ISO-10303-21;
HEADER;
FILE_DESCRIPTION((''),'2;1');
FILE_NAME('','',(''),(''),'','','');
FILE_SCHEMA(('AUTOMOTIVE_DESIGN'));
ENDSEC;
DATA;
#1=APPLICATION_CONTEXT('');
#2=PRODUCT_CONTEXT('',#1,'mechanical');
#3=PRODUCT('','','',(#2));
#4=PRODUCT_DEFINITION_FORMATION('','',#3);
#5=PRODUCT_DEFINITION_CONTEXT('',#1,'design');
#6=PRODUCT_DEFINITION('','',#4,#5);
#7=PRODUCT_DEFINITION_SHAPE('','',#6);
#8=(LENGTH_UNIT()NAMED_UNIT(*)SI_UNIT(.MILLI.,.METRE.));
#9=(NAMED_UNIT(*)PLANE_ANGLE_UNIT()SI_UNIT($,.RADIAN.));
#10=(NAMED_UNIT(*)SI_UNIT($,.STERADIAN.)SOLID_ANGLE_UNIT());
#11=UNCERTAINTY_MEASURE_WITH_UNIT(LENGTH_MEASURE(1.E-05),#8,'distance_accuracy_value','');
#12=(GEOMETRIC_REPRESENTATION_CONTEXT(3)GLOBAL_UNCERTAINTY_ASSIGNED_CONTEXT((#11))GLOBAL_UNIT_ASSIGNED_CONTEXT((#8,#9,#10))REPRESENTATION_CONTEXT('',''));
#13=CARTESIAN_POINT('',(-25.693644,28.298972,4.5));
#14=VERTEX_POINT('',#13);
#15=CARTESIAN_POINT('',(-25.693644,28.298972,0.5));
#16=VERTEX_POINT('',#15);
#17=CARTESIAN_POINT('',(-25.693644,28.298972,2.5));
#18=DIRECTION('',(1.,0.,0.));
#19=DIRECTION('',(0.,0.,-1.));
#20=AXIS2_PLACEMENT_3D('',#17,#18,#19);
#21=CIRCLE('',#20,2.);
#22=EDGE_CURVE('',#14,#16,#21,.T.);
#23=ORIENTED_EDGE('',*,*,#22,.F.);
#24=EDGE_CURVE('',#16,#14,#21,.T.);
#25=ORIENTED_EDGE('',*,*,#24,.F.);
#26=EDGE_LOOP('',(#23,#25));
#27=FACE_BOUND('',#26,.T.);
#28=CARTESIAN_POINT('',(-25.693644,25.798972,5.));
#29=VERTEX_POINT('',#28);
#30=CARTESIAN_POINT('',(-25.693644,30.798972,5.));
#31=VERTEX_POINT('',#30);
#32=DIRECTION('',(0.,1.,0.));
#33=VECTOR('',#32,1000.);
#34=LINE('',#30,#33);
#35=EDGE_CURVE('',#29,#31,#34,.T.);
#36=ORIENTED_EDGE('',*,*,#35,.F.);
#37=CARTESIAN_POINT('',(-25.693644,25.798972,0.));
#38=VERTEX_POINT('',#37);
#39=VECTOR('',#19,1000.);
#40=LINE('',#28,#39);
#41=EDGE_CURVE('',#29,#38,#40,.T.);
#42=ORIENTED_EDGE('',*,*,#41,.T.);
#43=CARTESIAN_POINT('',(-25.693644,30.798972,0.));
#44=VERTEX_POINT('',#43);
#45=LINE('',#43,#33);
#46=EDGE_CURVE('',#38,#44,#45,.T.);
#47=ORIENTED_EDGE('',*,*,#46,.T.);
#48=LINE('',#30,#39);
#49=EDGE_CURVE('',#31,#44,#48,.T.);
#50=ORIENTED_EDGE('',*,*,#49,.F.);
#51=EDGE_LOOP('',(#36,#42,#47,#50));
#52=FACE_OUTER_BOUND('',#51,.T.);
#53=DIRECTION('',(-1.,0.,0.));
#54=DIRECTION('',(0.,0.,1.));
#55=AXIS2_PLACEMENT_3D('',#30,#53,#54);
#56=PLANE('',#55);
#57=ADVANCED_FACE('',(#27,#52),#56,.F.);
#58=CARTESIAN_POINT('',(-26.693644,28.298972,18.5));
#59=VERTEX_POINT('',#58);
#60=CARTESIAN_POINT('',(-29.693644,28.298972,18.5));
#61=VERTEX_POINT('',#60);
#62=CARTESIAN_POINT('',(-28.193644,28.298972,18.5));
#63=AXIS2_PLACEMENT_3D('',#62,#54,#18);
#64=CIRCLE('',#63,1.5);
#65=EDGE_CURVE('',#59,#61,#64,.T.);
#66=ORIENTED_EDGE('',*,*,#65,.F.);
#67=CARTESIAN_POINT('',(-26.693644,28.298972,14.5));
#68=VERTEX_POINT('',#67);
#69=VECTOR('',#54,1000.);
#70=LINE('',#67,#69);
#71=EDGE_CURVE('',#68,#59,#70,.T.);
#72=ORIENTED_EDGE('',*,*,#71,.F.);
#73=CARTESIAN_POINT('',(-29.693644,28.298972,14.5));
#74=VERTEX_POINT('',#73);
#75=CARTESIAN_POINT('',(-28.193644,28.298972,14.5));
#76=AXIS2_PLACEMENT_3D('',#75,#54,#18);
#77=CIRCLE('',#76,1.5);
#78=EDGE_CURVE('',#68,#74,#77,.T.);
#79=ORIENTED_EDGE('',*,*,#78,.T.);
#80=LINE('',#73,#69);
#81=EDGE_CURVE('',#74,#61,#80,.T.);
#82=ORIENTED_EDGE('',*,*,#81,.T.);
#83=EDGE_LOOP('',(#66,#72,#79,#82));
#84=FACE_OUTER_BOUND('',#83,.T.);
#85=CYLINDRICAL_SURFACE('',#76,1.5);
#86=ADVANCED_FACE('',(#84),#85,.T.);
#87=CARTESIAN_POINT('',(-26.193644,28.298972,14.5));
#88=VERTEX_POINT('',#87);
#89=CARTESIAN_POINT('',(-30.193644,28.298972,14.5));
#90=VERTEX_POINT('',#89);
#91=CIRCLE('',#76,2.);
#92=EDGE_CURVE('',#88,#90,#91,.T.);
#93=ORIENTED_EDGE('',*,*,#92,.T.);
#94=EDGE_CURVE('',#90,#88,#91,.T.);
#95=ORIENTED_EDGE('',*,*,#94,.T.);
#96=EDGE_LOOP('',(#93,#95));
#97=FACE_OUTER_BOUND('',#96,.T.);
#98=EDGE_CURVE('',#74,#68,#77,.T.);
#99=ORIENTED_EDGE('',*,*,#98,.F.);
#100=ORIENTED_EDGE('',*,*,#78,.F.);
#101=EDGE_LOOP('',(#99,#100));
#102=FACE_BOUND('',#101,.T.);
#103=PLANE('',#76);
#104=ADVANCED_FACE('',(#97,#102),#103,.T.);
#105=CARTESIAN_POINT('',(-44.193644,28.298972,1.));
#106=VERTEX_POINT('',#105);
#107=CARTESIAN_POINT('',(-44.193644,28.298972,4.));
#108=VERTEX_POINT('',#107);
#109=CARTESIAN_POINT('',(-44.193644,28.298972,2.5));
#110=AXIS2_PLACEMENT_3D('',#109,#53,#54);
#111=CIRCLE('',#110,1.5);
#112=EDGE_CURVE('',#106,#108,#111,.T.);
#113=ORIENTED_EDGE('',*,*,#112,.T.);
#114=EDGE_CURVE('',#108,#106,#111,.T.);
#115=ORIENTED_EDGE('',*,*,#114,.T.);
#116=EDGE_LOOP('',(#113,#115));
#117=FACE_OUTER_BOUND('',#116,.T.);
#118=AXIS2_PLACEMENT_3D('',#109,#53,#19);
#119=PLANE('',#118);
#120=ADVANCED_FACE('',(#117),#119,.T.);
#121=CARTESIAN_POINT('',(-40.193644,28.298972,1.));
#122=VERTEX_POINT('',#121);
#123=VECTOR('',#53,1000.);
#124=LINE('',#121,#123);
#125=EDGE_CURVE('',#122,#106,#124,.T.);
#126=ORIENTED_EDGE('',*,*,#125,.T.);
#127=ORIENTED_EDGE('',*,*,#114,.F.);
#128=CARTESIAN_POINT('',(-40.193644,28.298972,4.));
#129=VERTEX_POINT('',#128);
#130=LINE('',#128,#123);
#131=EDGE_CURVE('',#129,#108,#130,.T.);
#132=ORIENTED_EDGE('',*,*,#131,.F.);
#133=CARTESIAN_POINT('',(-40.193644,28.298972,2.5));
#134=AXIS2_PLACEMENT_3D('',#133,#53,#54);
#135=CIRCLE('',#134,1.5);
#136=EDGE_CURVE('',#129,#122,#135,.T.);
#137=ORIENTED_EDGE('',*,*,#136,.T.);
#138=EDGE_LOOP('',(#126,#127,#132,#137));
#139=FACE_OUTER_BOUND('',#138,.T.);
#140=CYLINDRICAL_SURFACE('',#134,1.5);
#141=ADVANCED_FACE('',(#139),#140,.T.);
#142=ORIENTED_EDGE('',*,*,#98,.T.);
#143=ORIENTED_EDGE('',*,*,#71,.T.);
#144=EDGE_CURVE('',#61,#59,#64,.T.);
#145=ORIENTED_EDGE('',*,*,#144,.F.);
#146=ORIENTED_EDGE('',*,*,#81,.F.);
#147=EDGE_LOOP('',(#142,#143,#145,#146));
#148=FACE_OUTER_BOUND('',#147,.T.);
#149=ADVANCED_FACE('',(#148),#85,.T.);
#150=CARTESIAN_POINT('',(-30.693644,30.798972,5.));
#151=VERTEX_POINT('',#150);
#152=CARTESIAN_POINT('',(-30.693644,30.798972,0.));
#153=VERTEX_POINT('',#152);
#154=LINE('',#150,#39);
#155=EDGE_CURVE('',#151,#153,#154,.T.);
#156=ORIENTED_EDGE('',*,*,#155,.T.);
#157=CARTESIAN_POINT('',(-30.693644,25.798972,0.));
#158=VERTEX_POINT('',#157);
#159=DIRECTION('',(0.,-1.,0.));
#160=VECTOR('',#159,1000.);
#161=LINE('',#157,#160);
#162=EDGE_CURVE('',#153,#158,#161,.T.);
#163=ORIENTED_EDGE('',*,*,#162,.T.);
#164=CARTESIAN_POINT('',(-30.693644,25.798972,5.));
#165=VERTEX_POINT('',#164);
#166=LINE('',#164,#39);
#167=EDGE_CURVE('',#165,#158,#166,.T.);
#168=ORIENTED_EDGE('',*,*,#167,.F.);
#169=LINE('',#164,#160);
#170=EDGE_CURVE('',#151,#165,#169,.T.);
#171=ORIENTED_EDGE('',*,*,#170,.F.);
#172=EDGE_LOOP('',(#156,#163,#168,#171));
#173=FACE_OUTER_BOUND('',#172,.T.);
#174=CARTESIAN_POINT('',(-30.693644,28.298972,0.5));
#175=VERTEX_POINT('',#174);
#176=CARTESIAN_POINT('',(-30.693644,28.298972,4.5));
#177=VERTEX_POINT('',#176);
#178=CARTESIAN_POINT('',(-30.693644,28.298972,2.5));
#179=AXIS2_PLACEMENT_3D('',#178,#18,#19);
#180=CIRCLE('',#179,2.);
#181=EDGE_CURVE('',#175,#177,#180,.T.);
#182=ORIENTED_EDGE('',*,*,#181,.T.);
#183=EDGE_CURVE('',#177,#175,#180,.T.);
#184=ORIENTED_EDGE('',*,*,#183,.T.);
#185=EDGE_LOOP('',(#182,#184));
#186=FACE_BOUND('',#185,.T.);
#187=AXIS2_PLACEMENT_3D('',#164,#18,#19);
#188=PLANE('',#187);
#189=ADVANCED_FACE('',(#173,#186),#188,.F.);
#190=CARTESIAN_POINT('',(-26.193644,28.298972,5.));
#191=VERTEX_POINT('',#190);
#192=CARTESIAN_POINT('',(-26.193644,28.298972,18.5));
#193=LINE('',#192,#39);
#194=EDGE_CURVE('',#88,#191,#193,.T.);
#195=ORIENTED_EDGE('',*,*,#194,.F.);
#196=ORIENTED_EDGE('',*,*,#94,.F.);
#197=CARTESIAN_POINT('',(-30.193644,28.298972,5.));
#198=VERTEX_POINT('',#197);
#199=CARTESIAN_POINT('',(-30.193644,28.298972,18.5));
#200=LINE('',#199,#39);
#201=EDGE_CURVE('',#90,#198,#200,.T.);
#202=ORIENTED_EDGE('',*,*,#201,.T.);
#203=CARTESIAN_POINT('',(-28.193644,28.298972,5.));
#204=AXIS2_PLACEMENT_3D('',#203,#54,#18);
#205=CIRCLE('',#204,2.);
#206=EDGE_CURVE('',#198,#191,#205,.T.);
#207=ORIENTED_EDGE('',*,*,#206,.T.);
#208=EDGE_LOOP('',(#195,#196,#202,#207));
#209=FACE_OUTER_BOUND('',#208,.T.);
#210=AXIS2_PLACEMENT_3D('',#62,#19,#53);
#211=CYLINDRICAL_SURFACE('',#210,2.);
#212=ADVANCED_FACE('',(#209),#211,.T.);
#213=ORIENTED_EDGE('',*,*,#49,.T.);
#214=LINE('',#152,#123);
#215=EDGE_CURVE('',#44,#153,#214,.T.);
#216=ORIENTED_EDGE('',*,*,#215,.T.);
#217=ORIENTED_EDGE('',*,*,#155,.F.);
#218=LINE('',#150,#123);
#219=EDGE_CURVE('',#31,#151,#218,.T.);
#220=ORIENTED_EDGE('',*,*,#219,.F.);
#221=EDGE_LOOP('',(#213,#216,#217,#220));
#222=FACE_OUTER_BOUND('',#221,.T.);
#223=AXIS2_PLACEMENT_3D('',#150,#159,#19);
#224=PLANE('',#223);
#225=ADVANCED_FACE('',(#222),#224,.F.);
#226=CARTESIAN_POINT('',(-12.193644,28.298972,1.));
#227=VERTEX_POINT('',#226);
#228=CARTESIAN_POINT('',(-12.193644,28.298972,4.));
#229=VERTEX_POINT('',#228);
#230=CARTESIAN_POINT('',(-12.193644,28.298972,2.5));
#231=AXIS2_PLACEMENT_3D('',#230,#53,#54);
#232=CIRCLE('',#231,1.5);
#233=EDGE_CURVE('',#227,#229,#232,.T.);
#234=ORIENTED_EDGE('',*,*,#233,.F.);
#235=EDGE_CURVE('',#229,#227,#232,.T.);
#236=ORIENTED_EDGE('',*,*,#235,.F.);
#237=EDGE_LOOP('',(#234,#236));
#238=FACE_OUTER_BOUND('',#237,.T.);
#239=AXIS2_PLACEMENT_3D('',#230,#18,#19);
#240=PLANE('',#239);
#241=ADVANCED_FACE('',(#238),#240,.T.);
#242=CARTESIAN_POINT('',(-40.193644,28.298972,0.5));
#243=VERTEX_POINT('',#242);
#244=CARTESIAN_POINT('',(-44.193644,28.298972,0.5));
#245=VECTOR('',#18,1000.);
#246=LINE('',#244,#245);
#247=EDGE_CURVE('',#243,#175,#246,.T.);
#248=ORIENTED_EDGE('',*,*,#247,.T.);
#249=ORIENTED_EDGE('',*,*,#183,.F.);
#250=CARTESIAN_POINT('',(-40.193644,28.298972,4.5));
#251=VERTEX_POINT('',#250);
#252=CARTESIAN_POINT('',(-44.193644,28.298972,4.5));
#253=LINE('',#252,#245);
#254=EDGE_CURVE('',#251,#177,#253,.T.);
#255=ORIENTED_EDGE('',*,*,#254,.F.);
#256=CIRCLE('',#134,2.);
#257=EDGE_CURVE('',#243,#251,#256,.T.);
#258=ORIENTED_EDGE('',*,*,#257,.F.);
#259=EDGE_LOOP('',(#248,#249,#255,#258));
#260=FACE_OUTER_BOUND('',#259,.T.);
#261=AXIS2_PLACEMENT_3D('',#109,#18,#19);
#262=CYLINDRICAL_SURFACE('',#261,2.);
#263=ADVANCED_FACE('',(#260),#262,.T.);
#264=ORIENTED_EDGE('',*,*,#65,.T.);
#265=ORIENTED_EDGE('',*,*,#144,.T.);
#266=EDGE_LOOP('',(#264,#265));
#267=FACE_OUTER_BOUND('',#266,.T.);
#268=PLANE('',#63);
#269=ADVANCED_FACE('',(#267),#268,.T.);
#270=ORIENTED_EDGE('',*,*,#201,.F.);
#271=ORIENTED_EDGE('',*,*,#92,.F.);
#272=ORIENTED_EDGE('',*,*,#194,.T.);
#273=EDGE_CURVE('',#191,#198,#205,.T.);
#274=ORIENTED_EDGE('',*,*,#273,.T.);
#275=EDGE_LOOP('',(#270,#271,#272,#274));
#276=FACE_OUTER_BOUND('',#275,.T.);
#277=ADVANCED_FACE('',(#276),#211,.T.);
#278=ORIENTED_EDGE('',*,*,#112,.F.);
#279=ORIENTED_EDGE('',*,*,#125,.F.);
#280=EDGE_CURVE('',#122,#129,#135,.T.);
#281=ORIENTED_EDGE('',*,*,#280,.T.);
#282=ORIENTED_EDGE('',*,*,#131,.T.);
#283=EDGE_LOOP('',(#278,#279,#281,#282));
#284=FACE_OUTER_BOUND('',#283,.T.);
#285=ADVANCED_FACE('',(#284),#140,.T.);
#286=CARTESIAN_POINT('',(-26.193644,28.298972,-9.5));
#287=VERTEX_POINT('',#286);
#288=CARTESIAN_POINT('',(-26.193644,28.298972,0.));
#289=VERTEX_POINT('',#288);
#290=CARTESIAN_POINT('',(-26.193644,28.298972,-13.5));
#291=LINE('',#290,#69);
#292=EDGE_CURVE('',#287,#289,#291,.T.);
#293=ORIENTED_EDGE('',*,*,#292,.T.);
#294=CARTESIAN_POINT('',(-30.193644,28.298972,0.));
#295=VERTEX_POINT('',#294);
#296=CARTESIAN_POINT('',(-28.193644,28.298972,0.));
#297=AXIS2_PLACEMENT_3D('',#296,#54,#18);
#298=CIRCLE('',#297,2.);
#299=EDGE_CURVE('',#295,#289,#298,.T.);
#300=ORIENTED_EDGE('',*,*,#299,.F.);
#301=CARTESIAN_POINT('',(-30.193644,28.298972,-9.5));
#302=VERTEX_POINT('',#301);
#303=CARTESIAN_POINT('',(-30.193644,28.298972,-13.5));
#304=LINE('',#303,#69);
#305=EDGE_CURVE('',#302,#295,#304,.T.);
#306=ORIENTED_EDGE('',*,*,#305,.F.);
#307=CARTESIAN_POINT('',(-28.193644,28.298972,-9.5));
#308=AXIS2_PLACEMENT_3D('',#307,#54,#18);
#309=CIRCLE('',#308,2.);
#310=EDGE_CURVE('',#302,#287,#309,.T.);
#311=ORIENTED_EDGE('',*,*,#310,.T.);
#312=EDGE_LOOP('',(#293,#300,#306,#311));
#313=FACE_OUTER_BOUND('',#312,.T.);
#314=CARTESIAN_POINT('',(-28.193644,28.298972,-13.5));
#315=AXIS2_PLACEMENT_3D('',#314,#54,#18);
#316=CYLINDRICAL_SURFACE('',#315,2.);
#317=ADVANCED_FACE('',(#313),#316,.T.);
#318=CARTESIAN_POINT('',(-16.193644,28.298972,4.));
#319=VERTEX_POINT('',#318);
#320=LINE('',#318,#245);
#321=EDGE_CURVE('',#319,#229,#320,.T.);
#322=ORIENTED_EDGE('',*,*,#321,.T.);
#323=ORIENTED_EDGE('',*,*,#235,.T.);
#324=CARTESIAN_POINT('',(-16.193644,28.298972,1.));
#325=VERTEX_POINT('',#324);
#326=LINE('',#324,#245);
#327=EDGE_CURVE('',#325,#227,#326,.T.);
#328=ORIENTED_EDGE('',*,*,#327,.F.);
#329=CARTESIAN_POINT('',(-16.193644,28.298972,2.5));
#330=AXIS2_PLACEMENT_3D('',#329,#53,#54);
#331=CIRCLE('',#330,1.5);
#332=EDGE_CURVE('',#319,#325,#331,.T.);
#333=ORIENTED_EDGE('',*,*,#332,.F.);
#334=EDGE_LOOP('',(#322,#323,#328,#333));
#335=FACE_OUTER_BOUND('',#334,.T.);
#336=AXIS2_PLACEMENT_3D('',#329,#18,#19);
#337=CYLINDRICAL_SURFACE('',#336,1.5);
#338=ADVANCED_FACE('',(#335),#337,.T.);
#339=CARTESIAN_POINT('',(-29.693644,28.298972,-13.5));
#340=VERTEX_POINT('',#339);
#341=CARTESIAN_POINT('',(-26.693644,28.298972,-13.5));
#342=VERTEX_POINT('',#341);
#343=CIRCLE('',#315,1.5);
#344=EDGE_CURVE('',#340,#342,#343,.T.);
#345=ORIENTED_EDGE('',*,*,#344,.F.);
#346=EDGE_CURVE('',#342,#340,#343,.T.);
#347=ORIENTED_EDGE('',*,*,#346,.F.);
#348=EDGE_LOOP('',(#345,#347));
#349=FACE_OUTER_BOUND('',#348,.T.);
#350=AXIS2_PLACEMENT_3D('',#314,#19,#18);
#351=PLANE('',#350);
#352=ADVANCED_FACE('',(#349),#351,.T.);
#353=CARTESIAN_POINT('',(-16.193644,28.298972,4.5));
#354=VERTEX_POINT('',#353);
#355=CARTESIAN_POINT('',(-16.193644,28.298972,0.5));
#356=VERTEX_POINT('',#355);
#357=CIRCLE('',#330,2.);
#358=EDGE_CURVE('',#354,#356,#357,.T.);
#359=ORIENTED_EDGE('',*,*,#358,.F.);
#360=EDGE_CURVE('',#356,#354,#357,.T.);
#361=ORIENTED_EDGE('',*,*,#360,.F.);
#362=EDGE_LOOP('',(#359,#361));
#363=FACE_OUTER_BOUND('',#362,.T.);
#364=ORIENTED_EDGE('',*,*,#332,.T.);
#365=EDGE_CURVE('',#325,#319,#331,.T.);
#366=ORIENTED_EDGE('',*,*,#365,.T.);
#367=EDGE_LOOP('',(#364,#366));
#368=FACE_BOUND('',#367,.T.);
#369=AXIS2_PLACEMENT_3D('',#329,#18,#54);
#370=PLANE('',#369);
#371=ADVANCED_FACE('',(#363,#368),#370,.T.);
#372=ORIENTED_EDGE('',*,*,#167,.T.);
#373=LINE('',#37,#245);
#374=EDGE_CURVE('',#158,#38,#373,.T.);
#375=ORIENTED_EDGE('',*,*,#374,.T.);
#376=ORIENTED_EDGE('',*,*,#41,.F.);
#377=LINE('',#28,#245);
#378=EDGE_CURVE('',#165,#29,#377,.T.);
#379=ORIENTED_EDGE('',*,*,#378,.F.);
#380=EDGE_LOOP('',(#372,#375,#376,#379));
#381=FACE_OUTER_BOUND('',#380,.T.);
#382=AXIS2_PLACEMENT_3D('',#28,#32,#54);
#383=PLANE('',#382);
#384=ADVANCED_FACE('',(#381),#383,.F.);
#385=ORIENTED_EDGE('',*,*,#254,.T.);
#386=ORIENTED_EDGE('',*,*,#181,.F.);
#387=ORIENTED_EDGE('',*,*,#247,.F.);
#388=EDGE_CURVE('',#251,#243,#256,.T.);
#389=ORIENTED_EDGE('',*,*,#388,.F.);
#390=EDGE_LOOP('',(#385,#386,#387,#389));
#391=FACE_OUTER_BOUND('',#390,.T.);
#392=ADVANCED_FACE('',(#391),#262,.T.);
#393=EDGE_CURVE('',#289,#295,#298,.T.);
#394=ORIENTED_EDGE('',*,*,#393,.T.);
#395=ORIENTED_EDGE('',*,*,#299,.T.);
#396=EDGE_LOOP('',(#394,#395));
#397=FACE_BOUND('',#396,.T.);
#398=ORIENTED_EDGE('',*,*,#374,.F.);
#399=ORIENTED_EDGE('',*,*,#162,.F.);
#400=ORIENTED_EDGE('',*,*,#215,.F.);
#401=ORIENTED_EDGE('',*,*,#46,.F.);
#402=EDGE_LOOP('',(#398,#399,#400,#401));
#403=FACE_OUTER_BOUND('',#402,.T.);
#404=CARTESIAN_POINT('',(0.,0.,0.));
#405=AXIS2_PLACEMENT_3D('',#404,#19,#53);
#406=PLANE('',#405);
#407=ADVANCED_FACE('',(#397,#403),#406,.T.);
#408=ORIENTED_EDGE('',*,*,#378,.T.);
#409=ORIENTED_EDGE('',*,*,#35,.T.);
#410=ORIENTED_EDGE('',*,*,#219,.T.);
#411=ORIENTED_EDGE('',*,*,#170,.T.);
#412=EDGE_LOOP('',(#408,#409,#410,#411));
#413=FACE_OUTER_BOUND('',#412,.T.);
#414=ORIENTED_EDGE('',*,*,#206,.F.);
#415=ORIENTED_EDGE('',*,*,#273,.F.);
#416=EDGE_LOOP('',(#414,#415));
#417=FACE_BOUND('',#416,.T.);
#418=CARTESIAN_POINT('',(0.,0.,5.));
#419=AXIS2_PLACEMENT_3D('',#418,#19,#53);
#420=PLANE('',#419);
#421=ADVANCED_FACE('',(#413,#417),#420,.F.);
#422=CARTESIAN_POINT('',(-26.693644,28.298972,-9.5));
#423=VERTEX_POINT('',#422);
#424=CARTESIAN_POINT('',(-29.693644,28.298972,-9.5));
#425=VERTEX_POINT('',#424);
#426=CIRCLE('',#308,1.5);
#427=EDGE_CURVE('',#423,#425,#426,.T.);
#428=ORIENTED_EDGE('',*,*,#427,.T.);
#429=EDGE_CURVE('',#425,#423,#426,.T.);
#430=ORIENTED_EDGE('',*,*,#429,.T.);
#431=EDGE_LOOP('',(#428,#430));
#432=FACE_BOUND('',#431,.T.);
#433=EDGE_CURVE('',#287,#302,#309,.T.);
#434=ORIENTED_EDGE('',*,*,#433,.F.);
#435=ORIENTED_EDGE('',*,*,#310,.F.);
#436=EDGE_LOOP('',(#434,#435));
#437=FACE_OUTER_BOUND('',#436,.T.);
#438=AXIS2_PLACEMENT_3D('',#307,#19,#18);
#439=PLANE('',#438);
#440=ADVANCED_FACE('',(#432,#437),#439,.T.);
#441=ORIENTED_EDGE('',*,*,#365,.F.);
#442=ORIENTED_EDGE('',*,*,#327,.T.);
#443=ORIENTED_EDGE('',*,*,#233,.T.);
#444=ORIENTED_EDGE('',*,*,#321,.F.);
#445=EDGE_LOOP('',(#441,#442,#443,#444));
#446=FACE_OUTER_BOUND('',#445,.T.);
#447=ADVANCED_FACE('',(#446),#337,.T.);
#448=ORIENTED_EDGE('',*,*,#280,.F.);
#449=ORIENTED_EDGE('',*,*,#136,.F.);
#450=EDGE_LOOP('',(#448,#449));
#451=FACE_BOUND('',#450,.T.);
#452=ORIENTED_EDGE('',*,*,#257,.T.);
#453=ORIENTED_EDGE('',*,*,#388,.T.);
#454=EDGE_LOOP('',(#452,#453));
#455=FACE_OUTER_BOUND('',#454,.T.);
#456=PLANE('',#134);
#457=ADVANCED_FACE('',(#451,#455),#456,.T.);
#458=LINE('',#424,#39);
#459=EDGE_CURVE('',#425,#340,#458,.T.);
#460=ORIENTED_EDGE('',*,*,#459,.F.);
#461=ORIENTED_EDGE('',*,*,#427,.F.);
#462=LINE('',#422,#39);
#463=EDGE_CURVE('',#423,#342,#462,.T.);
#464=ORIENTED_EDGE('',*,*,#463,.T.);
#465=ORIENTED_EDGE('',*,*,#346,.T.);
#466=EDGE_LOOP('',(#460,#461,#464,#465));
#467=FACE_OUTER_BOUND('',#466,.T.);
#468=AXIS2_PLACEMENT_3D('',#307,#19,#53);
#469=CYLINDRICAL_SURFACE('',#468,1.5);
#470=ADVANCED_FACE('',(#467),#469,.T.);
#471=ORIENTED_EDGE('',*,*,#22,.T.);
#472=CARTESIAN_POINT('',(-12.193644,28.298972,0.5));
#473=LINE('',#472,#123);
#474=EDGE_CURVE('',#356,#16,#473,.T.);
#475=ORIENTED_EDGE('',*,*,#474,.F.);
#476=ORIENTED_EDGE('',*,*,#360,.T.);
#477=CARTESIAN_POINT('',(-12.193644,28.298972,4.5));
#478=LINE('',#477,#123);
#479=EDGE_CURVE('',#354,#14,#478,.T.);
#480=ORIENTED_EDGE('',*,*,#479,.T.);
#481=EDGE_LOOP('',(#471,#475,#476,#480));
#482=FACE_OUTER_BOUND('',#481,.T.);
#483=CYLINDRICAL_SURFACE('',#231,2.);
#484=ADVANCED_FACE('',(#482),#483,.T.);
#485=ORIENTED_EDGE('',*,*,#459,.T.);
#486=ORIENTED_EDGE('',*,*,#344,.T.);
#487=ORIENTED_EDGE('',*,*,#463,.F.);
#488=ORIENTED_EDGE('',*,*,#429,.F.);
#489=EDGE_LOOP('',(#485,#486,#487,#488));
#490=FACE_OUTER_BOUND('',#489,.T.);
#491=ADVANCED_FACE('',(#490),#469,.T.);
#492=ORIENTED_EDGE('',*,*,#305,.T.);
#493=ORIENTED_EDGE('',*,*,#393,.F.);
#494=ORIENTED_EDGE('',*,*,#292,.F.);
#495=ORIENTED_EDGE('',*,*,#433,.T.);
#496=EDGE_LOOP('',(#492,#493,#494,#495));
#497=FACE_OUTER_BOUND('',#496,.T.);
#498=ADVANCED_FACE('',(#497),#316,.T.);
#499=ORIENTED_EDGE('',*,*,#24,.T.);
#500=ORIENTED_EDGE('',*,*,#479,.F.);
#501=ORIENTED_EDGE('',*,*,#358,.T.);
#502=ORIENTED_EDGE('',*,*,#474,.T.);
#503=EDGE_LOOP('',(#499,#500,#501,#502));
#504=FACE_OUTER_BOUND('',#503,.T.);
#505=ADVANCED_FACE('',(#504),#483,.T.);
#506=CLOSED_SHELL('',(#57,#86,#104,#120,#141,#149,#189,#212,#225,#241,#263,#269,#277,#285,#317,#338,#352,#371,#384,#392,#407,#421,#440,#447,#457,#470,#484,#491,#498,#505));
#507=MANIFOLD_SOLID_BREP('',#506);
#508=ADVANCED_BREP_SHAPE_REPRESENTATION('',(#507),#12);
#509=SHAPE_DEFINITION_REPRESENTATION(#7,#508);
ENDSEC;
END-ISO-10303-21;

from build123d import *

# Parameters (mm, degrees)
SKETCH1_W           = 5
SKETCH1_H           = 5
BOSS_EXTRUDE1_DEPTH = 5
SKETCH2_R           = 2
BOSS_EXTRUDE2_DEPTH = 13.5
SKETCH3_R           = 2
BOSS_EXTRUDE3_DEPTH = 13.5
SKETCH4_R           = 2
SKETCH4_R_2         = 1.5
CUT_EXTRUDE1_DEPTH  = 4
SKETCH5_R           = 2
SKETCH5_R_2         = 1.5
CUT_EXTRUDE2_DEPTH  = 4


with BuildPart() as part:
    # Sketch1 → Boss-Extrude1 (new body)
    with BuildSketch(Plane.XY):
        with Locations((-28.193643968, 28.298971706)):
            Rectangle(SKETCH1_W, SKETCH1_H)
    extrude(amount=BOSS_EXTRUDE1_DEPTH)

    # Sketch2 → Boss-Extrude2 (add)
    with BuildSketch(Plane.XY.offset(5)):
        with Locations((-28.193643968, 28.298971706)):
            Circle(SKETCH2_R)
    boss_extrude2 = extrude(amount=BOSS_EXTRUDE2_DEPTH)

    # Sketch3 → Boss-Extrude3 (add)
    with BuildSketch(Plane(origin=(-25.693643968, 0, 0), x_dir=(0, 0, -1), z_dir=(1, 0, 0))):
        with Locations((-2.5, 28.298971706)):
            Circle(SKETCH3_R)
    boss_extrude3 = extrude(amount=BOSS_EXTRUDE3_DEPTH)

    # Mirror1: Boss-Extrude2 across plane
    add(boss_extrude2.mirror(Plane(origin=(0, 0, 2.5), x_dir=(1, 0, 0), z_dir=(0, 0, -1))))

    # Mirror2: Boss-Extrude3 across plane
    add(boss_extrude3.mirror(Plane(origin=(-28.193643968, 0, 0), x_dir=(0, 0, 1), z_dir=(1, 0, 0))))

    # Sketch4 → Cut-Extrude1 (cut)
    with BuildSketch(Plane.XY.offset(18.5)):
        with Locations((-28.193643968, 28.298971706)):
            Circle(SKETCH4_R)
        with Locations((-28.193643968, 28.298971706)):
            Circle(SKETCH4_R_2, mode=Mode.SUBTRACT)
    cut_extrude1 = extrude(amount=-CUT_EXTRUDE1_DEPTH, mode=Mode.SUBTRACT)

    # Mirror3: Cut-Extrude1 across plane
    add(cut_extrude1.mirror(Plane(origin=(0, 0, 2.5), x_dir=(1, 0, 0), z_dir=(0, 0, -1))), mode=Mode.SUBTRACT)

    # Sketch5 → Cut-Extrude2 (cut)
    with BuildSketch(Plane.ZY.offset(44.193643968)):
        with Locations(Location((2.5, 28.298971706, 0), (0, 0, 180))):
            Circle(SKETCH5_R)
        with Locations((2.5, 28.298971706)):
            Circle(SKETCH5_R_2, mode=Mode.SUBTRACT)
    cut_extrude2 = extrude(amount=-CUT_EXTRUDE2_DEPTH, mode=Mode.SUBTRACT)

    # Mirror4: Cut-Extrude2 across plane
    add(cut_extrude2.mirror(Plane(origin=(-28.193643968, 0, 0), x_dir=(0, 0, 1), z_dir=(1, 0, 0))), mode=Mode.SUBTRACT)


solid = part.part
